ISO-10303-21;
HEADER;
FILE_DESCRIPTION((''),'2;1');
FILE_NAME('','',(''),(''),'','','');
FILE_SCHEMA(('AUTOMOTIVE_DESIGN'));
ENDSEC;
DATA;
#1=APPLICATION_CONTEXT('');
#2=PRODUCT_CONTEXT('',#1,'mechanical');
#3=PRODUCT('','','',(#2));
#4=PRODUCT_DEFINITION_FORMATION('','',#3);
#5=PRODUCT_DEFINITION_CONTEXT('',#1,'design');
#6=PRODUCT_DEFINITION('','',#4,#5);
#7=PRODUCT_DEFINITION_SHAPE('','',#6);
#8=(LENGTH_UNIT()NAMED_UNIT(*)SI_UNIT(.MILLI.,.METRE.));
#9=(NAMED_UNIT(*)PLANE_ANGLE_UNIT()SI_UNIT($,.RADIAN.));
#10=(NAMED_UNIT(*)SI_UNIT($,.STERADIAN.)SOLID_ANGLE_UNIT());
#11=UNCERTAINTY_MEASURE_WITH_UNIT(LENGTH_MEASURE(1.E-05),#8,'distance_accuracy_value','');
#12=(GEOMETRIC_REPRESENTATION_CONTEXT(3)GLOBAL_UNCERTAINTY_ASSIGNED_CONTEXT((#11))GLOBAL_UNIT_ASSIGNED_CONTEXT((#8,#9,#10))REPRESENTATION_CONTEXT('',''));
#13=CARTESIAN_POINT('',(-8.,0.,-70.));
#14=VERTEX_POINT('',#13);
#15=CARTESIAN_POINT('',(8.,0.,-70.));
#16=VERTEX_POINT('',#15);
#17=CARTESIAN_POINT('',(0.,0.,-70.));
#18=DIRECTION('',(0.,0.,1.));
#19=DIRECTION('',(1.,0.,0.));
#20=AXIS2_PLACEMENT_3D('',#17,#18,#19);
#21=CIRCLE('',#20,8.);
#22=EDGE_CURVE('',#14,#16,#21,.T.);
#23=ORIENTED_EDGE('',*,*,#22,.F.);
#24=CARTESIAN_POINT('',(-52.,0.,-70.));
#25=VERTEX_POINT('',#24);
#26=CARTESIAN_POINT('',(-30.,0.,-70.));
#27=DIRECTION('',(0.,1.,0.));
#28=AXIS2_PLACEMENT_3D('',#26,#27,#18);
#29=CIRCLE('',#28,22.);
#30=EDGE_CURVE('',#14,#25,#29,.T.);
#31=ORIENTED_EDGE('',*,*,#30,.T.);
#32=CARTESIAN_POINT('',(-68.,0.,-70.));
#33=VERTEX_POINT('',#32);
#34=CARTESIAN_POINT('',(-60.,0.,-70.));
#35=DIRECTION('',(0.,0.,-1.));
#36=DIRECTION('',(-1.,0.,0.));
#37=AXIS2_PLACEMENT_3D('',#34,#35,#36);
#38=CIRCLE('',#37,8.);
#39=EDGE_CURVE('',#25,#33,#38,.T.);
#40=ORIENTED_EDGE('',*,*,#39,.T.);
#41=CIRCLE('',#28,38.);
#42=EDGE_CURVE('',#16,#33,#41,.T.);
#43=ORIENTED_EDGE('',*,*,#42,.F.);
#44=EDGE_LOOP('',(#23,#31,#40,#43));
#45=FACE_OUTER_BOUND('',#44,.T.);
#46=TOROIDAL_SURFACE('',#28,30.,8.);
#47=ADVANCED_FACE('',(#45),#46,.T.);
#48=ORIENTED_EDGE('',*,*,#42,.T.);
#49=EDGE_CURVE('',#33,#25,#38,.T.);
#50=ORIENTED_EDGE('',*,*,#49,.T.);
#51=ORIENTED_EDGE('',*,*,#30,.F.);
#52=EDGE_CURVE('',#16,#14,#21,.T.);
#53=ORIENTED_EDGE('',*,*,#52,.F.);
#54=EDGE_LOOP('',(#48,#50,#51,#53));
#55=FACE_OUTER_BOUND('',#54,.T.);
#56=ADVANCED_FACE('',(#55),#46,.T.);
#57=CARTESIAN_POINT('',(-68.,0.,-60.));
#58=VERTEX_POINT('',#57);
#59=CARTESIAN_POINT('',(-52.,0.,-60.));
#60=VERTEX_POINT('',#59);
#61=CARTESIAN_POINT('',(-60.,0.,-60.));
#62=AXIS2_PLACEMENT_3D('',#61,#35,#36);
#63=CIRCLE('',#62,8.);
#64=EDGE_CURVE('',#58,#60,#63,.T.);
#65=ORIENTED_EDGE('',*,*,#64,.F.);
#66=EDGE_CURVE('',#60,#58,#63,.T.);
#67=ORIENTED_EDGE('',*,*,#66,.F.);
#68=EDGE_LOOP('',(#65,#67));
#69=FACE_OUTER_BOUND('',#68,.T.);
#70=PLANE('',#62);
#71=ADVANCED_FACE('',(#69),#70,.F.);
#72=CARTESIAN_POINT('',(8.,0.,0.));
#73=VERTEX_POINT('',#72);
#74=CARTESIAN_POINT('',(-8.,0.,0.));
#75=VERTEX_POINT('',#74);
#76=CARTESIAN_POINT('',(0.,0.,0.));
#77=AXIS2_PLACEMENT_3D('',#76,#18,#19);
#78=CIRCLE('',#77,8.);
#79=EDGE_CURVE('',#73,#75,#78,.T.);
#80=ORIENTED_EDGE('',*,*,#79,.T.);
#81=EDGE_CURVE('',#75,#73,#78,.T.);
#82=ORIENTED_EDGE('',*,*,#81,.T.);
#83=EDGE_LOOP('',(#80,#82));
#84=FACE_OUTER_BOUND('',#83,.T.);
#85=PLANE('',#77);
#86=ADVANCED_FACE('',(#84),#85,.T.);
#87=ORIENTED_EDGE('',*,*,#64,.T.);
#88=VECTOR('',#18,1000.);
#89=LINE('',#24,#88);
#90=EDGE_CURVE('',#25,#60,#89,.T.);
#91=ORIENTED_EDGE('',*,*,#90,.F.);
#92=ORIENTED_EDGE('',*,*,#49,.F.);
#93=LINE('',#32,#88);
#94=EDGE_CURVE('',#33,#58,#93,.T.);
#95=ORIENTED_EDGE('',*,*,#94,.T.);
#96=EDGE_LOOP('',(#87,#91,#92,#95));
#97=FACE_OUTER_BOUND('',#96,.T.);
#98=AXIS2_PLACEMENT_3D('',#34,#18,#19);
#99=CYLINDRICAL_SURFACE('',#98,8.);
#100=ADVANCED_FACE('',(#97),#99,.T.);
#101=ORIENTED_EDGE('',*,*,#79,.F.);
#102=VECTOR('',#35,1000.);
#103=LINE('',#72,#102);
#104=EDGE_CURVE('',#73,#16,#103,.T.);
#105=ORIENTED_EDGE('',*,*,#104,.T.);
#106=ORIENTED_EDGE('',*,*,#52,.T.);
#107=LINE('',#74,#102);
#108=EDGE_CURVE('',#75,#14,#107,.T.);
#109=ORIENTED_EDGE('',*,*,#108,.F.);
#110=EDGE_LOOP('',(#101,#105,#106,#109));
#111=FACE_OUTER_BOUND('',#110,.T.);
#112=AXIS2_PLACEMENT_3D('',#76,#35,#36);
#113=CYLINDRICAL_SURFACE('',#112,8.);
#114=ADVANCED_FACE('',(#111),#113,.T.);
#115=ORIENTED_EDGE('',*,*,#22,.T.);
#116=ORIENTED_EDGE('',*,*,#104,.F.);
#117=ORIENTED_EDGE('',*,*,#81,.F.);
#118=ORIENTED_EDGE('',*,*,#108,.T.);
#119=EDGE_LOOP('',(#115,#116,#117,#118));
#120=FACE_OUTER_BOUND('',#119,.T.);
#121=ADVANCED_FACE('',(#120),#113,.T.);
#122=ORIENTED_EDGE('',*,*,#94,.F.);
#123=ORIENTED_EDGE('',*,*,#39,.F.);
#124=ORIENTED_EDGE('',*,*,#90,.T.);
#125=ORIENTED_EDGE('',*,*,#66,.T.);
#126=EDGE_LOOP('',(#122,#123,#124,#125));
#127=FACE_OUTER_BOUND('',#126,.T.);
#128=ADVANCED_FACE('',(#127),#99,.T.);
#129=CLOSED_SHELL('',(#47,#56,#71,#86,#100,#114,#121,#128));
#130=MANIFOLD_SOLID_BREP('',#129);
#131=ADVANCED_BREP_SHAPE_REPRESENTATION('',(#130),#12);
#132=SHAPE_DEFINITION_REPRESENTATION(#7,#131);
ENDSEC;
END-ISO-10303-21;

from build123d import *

# Parameters (mm, degrees)
SKETCH1_R = 8


with BuildPart() as part:
    # Sweep1: sweep along a path in Sketch2
    with BuildLine(Plane(origin=(0, 0, 0), x_dir=(1, 0, 0), z_dir=(0, 1, 0))) as sweep1_path:
        Line((0, 0), (0, 70))
        ThreePointArc((0, 70), (-30, 100), (-60, 70))
        Line((-60, 70), (-60, 60))
    # Sketch1 → Sweep1 (sweep)
    with BuildSketch(Plane.XY):
        Circle(SKETCH1_R)
    sweep(path=sweep1_path.line)


solid = part.part
